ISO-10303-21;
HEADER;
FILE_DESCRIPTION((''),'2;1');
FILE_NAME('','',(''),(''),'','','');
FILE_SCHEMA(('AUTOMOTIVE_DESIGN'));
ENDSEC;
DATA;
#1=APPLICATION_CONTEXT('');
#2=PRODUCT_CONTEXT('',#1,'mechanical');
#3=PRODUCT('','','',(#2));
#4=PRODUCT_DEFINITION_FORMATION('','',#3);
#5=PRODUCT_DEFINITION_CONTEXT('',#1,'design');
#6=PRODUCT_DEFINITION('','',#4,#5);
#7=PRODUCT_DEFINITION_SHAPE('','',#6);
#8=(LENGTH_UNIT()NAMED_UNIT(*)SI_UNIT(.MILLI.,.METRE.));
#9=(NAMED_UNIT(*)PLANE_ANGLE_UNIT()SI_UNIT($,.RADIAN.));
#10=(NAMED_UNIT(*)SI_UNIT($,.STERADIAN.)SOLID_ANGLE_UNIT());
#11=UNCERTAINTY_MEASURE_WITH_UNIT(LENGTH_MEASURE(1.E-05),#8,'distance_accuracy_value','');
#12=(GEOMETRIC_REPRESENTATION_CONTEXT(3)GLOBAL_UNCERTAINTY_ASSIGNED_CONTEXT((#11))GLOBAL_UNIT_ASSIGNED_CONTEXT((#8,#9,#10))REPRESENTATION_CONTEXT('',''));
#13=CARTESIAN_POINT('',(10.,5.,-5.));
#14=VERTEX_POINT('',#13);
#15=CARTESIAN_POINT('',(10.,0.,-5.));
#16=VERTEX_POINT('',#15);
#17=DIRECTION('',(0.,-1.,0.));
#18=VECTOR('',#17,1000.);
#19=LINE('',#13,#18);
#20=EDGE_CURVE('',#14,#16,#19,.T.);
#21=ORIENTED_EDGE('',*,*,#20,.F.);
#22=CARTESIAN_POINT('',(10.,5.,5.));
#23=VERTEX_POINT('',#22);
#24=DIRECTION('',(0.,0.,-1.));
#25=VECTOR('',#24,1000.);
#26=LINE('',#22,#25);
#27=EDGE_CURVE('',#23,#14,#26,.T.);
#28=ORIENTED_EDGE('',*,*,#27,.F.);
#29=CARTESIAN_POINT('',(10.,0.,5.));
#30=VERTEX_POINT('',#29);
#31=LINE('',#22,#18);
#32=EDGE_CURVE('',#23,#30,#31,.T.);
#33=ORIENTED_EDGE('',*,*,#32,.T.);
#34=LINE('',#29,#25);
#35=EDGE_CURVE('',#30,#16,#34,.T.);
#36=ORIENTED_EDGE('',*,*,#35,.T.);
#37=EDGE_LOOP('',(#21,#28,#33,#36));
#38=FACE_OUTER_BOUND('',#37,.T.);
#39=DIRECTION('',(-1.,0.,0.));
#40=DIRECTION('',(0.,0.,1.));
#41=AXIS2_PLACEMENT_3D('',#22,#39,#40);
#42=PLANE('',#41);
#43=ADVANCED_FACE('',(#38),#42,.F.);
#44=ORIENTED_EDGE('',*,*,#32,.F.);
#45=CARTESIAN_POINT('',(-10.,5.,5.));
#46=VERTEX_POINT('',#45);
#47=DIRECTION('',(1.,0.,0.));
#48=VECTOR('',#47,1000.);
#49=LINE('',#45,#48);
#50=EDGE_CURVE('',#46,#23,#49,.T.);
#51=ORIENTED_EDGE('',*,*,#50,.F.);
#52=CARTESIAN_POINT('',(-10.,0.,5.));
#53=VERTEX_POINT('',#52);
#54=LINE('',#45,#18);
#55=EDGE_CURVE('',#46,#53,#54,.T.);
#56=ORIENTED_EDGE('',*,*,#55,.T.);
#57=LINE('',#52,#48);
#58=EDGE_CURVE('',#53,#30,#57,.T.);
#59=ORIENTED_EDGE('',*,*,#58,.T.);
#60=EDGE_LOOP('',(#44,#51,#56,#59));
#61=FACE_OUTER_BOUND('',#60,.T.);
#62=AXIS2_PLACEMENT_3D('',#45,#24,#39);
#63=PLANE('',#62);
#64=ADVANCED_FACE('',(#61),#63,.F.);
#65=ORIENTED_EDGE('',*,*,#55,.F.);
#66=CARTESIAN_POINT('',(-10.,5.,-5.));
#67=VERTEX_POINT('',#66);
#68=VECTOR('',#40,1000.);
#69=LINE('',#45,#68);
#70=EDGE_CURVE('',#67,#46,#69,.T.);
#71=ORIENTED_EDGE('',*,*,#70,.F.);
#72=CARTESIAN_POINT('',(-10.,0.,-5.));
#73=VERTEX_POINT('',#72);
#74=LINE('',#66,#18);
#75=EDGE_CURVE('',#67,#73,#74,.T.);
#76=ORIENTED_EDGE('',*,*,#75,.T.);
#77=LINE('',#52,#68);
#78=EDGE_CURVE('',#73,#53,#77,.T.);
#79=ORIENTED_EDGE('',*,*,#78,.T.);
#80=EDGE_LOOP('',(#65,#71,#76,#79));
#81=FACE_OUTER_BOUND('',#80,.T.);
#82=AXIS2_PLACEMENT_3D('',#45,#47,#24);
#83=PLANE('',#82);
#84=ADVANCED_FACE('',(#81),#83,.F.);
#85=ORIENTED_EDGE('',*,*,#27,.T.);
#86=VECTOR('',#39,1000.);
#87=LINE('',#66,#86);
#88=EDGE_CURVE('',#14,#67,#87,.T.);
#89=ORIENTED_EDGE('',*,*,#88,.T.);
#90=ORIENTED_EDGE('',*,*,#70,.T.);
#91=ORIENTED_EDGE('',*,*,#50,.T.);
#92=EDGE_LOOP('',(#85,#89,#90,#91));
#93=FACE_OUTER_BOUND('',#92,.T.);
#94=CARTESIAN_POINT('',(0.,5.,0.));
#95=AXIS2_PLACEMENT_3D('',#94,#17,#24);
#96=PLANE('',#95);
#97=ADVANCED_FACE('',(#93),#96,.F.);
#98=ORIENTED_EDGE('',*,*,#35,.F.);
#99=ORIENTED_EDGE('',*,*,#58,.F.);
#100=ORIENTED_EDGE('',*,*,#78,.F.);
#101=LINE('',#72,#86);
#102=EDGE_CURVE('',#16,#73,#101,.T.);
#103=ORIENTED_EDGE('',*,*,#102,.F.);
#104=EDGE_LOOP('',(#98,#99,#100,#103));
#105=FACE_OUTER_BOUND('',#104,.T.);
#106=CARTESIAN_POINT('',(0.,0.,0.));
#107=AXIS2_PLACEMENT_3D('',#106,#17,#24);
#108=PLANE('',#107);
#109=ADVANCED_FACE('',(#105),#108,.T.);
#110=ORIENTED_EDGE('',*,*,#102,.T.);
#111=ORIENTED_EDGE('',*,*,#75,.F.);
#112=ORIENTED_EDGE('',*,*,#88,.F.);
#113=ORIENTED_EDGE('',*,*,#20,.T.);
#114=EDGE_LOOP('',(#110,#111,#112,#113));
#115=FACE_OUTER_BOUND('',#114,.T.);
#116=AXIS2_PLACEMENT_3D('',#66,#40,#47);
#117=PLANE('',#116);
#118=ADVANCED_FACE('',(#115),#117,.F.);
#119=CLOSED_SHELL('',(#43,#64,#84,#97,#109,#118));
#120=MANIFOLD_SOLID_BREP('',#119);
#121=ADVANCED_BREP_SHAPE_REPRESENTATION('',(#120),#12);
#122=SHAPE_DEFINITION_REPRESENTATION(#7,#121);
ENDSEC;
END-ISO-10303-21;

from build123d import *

# Parameters (mm, degrees)
SKETCH1_W           = 20
SKETCH1_H           = 10
BOSS_EXTRUDE1_DEPTH = 5


with BuildPart() as part:
    # Sketch1 → Boss-Extrude1 (new body)
    with BuildSketch(Plane(origin=(0, 0, 0), x_dir=(1, 0, 0), z_dir=(0, 1, 0))):
        Rectangle(SKETCH1_W, SKETCH1_H)
    extrude(amount=BOSS_EXTRUDE1_DEPTH)


solid = part.part
